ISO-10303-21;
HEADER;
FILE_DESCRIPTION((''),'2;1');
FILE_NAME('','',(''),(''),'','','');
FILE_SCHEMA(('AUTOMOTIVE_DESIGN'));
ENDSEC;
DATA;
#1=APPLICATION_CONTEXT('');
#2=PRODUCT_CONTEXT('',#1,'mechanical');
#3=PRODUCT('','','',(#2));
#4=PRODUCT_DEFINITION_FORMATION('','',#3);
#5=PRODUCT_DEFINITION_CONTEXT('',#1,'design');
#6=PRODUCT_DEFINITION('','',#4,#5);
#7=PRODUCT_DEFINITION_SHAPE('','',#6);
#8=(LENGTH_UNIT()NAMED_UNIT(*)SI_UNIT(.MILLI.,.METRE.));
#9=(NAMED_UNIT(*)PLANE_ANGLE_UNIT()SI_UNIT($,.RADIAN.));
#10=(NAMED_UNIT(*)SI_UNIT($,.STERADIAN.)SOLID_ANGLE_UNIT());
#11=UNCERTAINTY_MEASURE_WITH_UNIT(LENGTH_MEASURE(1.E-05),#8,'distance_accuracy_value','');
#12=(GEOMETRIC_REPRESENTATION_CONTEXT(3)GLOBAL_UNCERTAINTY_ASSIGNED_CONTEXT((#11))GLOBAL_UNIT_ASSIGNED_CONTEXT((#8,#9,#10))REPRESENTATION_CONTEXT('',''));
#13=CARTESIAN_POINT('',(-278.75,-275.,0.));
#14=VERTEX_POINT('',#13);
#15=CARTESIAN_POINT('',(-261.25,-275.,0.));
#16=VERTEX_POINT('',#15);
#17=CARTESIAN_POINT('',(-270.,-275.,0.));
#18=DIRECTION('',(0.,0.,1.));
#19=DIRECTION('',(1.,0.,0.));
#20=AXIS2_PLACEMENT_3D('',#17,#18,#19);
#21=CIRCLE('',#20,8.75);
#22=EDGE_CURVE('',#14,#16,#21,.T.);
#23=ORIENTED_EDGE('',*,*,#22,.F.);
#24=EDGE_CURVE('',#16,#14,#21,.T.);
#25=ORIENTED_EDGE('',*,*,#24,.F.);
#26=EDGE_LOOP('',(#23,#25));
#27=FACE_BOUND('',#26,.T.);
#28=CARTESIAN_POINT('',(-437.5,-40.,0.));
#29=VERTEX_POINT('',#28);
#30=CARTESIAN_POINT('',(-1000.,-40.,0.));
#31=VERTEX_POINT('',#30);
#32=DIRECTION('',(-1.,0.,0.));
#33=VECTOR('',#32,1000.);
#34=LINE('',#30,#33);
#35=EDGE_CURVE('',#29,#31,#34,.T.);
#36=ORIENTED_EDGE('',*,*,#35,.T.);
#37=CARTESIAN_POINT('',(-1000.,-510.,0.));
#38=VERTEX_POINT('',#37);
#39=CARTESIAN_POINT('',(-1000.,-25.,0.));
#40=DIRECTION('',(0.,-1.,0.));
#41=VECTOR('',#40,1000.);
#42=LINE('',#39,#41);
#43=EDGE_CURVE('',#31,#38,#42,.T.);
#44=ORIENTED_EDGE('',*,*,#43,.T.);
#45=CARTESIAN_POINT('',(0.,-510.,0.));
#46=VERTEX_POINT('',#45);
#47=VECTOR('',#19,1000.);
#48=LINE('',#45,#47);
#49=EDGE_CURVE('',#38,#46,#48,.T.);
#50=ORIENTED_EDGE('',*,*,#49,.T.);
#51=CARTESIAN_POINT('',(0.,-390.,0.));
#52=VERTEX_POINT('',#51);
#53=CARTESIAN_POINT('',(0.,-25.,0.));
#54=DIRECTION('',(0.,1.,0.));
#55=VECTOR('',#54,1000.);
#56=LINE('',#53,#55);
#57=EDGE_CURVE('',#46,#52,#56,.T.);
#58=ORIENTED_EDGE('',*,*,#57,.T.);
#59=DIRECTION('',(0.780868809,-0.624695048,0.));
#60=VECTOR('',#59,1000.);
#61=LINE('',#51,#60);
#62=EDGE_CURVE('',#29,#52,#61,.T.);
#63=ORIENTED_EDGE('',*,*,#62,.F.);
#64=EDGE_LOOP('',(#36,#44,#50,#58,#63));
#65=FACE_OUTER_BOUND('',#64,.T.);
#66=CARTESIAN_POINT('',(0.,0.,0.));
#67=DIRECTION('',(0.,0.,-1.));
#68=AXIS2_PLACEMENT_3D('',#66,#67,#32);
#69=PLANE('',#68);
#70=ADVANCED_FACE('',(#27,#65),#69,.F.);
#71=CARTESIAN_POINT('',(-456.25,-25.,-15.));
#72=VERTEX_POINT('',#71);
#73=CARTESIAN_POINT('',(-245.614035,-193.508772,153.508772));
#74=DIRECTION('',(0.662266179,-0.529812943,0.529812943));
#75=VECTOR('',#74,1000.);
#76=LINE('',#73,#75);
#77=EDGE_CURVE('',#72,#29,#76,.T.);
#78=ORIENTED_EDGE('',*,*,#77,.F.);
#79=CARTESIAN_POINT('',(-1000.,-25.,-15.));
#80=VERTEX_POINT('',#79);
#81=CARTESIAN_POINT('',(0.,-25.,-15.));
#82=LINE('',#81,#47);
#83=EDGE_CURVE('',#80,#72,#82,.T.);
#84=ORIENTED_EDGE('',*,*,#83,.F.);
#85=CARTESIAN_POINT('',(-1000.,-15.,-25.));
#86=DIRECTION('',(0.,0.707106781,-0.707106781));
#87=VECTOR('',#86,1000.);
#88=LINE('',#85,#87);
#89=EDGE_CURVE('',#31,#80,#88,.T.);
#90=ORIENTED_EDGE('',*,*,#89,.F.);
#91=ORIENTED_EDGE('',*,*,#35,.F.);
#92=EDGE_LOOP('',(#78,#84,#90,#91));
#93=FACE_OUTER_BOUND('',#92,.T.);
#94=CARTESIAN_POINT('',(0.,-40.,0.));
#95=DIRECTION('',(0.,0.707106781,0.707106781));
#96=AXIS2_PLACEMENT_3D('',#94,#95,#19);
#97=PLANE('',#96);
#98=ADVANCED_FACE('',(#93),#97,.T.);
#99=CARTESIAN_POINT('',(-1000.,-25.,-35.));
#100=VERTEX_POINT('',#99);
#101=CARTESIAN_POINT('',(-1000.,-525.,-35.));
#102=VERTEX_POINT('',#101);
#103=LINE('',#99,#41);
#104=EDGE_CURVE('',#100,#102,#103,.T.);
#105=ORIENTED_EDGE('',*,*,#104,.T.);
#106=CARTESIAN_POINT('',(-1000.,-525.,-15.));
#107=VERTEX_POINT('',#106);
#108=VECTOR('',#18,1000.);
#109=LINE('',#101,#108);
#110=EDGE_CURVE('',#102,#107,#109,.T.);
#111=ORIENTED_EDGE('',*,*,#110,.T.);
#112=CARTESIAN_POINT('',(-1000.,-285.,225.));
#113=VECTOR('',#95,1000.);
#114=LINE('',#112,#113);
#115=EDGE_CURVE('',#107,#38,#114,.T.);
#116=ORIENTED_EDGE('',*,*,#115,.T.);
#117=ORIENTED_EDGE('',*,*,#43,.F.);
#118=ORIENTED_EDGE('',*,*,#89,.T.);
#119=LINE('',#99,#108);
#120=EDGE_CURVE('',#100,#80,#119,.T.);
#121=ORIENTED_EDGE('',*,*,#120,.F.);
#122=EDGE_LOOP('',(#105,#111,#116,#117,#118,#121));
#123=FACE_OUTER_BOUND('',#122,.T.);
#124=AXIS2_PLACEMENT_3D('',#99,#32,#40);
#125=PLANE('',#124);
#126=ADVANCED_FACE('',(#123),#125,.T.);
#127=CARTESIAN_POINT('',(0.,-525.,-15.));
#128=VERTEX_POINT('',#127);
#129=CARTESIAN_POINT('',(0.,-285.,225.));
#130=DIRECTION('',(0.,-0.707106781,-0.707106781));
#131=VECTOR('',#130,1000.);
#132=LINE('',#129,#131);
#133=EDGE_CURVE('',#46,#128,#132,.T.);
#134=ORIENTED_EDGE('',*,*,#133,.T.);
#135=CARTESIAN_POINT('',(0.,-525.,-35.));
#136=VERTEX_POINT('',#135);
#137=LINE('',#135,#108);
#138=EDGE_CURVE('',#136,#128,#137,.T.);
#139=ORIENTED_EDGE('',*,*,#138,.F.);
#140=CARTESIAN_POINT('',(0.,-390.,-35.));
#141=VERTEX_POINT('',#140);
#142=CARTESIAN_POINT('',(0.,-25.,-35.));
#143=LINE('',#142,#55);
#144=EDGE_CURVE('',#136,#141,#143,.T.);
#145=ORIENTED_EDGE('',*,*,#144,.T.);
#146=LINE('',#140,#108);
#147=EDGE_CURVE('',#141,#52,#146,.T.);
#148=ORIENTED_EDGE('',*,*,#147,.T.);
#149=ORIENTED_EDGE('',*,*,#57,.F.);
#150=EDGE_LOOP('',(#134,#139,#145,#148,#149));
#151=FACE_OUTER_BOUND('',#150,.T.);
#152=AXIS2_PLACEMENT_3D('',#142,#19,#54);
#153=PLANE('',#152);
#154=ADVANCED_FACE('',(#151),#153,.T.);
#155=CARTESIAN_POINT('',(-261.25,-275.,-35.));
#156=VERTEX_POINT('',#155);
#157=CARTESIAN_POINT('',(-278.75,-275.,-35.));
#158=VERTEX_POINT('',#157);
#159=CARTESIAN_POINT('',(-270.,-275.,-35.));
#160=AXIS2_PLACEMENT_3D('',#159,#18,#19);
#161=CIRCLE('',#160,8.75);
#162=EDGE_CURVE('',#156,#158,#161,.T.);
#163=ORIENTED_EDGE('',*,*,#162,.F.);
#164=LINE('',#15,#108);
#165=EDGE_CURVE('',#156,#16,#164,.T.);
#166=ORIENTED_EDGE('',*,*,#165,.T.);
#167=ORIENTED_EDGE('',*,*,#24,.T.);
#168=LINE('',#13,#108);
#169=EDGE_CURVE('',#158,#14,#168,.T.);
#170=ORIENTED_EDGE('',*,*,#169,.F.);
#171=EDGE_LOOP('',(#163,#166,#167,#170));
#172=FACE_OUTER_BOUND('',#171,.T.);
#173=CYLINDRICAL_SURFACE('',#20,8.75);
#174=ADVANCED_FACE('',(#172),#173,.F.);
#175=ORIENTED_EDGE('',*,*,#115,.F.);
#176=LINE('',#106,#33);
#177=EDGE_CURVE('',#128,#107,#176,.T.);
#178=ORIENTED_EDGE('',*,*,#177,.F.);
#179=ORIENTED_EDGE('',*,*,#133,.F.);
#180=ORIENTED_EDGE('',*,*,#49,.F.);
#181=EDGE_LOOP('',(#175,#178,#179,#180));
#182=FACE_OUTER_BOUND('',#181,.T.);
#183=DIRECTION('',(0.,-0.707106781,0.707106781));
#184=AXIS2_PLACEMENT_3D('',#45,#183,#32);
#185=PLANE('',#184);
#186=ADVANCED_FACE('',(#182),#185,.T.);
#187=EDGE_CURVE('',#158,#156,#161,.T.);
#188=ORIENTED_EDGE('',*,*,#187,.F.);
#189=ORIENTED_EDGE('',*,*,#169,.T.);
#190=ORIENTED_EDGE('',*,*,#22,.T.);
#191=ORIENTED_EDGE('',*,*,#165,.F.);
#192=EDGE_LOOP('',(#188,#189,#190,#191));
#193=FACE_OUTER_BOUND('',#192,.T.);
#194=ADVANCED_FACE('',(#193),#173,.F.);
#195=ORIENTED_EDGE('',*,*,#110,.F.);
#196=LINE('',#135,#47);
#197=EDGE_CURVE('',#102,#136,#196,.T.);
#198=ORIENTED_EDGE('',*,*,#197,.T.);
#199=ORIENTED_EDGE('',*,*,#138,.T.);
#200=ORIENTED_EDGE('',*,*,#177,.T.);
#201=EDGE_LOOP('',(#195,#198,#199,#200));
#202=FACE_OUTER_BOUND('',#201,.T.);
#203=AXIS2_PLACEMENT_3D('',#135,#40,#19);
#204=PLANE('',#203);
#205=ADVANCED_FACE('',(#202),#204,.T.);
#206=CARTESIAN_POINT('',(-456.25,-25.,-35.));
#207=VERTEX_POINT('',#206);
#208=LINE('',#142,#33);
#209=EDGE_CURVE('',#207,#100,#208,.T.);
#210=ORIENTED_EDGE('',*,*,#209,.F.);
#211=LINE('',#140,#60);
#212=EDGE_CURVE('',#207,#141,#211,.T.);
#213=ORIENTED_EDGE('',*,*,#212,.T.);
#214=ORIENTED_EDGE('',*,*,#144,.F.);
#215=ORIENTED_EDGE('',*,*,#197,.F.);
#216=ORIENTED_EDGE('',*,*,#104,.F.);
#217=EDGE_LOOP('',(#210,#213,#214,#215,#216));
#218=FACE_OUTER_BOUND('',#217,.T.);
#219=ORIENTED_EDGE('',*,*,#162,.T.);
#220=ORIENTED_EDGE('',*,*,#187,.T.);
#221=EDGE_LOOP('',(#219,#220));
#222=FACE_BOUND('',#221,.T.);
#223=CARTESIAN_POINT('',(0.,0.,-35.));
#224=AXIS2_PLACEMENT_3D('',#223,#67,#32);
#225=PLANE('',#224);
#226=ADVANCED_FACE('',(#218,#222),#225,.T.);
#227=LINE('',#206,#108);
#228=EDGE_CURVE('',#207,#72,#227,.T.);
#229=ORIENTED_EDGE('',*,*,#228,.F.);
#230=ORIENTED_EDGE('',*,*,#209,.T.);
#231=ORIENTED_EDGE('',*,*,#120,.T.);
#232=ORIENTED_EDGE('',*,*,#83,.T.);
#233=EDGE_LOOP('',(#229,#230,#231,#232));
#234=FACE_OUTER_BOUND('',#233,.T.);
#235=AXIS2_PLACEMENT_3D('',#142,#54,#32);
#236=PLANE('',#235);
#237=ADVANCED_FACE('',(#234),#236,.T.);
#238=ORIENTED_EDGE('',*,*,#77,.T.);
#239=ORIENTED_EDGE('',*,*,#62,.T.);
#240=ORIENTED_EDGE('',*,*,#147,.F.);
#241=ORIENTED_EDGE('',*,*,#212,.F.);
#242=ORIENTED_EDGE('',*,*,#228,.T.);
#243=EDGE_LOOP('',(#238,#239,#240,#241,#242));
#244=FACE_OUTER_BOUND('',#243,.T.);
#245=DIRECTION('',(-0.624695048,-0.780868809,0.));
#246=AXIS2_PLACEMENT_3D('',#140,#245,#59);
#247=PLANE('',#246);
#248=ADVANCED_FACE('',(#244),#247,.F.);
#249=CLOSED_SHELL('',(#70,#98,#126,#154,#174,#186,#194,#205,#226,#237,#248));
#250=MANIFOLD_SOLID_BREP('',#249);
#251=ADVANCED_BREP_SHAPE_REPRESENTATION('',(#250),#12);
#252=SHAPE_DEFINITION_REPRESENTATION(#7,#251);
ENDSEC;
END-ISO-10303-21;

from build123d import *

# Parameters (mm, degrees)
SKETCH1_W           = 1000
SKETCH1_H           = 500
BOSS_EXTRUDE1_DEPTH = 35
M20_TAPPED_HOLE1_D  = 17.5
CHAMFER1_SIZE       = 15
CUT_EXTRUDE3_DEPTH  = 1130.97787589


with BuildPart() as part:
    # Sketch1 → Boss-Extrude1 (new body)
    with BuildSketch(Plane.XY):
        with Locations((-500, -275)):
            Rectangle(SKETCH1_W, SKETCH1_H)
    extrude(amount=-BOSS_EXTRUDE1_DEPTH)

    # M20 Tapped Hole1 (through all)
    with Locations(Plane(origin=(-30, -275, 0), x_dir=(1, 0, 0), z_dir=(0, 0, 1))):
        with Locations((0, 0), (-240, 0)):
            Hole(M20_TAPPED_HOLE1_D / 2)

    # Chamfer1
    chamfer1_edges = [part.edges().sort_by_distance(p)[0] for p in [
        (-500, -525, 0),
        (-500, -25, 0),
    ]]
    chamfer(chamfer1_edges, length=CHAMFER1_SIZE)

    # Sketch9 → Cut-Extrude3 (cut, through all)
    with BuildSketch(Plane.XY):
        Polygon((-500, 10), (0, 10), (0, -390), align=None)
    extrude(amount=-CUT_EXTRUDE3_DEPTH, mode=Mode.SUBTRACT)


solid = part.part
